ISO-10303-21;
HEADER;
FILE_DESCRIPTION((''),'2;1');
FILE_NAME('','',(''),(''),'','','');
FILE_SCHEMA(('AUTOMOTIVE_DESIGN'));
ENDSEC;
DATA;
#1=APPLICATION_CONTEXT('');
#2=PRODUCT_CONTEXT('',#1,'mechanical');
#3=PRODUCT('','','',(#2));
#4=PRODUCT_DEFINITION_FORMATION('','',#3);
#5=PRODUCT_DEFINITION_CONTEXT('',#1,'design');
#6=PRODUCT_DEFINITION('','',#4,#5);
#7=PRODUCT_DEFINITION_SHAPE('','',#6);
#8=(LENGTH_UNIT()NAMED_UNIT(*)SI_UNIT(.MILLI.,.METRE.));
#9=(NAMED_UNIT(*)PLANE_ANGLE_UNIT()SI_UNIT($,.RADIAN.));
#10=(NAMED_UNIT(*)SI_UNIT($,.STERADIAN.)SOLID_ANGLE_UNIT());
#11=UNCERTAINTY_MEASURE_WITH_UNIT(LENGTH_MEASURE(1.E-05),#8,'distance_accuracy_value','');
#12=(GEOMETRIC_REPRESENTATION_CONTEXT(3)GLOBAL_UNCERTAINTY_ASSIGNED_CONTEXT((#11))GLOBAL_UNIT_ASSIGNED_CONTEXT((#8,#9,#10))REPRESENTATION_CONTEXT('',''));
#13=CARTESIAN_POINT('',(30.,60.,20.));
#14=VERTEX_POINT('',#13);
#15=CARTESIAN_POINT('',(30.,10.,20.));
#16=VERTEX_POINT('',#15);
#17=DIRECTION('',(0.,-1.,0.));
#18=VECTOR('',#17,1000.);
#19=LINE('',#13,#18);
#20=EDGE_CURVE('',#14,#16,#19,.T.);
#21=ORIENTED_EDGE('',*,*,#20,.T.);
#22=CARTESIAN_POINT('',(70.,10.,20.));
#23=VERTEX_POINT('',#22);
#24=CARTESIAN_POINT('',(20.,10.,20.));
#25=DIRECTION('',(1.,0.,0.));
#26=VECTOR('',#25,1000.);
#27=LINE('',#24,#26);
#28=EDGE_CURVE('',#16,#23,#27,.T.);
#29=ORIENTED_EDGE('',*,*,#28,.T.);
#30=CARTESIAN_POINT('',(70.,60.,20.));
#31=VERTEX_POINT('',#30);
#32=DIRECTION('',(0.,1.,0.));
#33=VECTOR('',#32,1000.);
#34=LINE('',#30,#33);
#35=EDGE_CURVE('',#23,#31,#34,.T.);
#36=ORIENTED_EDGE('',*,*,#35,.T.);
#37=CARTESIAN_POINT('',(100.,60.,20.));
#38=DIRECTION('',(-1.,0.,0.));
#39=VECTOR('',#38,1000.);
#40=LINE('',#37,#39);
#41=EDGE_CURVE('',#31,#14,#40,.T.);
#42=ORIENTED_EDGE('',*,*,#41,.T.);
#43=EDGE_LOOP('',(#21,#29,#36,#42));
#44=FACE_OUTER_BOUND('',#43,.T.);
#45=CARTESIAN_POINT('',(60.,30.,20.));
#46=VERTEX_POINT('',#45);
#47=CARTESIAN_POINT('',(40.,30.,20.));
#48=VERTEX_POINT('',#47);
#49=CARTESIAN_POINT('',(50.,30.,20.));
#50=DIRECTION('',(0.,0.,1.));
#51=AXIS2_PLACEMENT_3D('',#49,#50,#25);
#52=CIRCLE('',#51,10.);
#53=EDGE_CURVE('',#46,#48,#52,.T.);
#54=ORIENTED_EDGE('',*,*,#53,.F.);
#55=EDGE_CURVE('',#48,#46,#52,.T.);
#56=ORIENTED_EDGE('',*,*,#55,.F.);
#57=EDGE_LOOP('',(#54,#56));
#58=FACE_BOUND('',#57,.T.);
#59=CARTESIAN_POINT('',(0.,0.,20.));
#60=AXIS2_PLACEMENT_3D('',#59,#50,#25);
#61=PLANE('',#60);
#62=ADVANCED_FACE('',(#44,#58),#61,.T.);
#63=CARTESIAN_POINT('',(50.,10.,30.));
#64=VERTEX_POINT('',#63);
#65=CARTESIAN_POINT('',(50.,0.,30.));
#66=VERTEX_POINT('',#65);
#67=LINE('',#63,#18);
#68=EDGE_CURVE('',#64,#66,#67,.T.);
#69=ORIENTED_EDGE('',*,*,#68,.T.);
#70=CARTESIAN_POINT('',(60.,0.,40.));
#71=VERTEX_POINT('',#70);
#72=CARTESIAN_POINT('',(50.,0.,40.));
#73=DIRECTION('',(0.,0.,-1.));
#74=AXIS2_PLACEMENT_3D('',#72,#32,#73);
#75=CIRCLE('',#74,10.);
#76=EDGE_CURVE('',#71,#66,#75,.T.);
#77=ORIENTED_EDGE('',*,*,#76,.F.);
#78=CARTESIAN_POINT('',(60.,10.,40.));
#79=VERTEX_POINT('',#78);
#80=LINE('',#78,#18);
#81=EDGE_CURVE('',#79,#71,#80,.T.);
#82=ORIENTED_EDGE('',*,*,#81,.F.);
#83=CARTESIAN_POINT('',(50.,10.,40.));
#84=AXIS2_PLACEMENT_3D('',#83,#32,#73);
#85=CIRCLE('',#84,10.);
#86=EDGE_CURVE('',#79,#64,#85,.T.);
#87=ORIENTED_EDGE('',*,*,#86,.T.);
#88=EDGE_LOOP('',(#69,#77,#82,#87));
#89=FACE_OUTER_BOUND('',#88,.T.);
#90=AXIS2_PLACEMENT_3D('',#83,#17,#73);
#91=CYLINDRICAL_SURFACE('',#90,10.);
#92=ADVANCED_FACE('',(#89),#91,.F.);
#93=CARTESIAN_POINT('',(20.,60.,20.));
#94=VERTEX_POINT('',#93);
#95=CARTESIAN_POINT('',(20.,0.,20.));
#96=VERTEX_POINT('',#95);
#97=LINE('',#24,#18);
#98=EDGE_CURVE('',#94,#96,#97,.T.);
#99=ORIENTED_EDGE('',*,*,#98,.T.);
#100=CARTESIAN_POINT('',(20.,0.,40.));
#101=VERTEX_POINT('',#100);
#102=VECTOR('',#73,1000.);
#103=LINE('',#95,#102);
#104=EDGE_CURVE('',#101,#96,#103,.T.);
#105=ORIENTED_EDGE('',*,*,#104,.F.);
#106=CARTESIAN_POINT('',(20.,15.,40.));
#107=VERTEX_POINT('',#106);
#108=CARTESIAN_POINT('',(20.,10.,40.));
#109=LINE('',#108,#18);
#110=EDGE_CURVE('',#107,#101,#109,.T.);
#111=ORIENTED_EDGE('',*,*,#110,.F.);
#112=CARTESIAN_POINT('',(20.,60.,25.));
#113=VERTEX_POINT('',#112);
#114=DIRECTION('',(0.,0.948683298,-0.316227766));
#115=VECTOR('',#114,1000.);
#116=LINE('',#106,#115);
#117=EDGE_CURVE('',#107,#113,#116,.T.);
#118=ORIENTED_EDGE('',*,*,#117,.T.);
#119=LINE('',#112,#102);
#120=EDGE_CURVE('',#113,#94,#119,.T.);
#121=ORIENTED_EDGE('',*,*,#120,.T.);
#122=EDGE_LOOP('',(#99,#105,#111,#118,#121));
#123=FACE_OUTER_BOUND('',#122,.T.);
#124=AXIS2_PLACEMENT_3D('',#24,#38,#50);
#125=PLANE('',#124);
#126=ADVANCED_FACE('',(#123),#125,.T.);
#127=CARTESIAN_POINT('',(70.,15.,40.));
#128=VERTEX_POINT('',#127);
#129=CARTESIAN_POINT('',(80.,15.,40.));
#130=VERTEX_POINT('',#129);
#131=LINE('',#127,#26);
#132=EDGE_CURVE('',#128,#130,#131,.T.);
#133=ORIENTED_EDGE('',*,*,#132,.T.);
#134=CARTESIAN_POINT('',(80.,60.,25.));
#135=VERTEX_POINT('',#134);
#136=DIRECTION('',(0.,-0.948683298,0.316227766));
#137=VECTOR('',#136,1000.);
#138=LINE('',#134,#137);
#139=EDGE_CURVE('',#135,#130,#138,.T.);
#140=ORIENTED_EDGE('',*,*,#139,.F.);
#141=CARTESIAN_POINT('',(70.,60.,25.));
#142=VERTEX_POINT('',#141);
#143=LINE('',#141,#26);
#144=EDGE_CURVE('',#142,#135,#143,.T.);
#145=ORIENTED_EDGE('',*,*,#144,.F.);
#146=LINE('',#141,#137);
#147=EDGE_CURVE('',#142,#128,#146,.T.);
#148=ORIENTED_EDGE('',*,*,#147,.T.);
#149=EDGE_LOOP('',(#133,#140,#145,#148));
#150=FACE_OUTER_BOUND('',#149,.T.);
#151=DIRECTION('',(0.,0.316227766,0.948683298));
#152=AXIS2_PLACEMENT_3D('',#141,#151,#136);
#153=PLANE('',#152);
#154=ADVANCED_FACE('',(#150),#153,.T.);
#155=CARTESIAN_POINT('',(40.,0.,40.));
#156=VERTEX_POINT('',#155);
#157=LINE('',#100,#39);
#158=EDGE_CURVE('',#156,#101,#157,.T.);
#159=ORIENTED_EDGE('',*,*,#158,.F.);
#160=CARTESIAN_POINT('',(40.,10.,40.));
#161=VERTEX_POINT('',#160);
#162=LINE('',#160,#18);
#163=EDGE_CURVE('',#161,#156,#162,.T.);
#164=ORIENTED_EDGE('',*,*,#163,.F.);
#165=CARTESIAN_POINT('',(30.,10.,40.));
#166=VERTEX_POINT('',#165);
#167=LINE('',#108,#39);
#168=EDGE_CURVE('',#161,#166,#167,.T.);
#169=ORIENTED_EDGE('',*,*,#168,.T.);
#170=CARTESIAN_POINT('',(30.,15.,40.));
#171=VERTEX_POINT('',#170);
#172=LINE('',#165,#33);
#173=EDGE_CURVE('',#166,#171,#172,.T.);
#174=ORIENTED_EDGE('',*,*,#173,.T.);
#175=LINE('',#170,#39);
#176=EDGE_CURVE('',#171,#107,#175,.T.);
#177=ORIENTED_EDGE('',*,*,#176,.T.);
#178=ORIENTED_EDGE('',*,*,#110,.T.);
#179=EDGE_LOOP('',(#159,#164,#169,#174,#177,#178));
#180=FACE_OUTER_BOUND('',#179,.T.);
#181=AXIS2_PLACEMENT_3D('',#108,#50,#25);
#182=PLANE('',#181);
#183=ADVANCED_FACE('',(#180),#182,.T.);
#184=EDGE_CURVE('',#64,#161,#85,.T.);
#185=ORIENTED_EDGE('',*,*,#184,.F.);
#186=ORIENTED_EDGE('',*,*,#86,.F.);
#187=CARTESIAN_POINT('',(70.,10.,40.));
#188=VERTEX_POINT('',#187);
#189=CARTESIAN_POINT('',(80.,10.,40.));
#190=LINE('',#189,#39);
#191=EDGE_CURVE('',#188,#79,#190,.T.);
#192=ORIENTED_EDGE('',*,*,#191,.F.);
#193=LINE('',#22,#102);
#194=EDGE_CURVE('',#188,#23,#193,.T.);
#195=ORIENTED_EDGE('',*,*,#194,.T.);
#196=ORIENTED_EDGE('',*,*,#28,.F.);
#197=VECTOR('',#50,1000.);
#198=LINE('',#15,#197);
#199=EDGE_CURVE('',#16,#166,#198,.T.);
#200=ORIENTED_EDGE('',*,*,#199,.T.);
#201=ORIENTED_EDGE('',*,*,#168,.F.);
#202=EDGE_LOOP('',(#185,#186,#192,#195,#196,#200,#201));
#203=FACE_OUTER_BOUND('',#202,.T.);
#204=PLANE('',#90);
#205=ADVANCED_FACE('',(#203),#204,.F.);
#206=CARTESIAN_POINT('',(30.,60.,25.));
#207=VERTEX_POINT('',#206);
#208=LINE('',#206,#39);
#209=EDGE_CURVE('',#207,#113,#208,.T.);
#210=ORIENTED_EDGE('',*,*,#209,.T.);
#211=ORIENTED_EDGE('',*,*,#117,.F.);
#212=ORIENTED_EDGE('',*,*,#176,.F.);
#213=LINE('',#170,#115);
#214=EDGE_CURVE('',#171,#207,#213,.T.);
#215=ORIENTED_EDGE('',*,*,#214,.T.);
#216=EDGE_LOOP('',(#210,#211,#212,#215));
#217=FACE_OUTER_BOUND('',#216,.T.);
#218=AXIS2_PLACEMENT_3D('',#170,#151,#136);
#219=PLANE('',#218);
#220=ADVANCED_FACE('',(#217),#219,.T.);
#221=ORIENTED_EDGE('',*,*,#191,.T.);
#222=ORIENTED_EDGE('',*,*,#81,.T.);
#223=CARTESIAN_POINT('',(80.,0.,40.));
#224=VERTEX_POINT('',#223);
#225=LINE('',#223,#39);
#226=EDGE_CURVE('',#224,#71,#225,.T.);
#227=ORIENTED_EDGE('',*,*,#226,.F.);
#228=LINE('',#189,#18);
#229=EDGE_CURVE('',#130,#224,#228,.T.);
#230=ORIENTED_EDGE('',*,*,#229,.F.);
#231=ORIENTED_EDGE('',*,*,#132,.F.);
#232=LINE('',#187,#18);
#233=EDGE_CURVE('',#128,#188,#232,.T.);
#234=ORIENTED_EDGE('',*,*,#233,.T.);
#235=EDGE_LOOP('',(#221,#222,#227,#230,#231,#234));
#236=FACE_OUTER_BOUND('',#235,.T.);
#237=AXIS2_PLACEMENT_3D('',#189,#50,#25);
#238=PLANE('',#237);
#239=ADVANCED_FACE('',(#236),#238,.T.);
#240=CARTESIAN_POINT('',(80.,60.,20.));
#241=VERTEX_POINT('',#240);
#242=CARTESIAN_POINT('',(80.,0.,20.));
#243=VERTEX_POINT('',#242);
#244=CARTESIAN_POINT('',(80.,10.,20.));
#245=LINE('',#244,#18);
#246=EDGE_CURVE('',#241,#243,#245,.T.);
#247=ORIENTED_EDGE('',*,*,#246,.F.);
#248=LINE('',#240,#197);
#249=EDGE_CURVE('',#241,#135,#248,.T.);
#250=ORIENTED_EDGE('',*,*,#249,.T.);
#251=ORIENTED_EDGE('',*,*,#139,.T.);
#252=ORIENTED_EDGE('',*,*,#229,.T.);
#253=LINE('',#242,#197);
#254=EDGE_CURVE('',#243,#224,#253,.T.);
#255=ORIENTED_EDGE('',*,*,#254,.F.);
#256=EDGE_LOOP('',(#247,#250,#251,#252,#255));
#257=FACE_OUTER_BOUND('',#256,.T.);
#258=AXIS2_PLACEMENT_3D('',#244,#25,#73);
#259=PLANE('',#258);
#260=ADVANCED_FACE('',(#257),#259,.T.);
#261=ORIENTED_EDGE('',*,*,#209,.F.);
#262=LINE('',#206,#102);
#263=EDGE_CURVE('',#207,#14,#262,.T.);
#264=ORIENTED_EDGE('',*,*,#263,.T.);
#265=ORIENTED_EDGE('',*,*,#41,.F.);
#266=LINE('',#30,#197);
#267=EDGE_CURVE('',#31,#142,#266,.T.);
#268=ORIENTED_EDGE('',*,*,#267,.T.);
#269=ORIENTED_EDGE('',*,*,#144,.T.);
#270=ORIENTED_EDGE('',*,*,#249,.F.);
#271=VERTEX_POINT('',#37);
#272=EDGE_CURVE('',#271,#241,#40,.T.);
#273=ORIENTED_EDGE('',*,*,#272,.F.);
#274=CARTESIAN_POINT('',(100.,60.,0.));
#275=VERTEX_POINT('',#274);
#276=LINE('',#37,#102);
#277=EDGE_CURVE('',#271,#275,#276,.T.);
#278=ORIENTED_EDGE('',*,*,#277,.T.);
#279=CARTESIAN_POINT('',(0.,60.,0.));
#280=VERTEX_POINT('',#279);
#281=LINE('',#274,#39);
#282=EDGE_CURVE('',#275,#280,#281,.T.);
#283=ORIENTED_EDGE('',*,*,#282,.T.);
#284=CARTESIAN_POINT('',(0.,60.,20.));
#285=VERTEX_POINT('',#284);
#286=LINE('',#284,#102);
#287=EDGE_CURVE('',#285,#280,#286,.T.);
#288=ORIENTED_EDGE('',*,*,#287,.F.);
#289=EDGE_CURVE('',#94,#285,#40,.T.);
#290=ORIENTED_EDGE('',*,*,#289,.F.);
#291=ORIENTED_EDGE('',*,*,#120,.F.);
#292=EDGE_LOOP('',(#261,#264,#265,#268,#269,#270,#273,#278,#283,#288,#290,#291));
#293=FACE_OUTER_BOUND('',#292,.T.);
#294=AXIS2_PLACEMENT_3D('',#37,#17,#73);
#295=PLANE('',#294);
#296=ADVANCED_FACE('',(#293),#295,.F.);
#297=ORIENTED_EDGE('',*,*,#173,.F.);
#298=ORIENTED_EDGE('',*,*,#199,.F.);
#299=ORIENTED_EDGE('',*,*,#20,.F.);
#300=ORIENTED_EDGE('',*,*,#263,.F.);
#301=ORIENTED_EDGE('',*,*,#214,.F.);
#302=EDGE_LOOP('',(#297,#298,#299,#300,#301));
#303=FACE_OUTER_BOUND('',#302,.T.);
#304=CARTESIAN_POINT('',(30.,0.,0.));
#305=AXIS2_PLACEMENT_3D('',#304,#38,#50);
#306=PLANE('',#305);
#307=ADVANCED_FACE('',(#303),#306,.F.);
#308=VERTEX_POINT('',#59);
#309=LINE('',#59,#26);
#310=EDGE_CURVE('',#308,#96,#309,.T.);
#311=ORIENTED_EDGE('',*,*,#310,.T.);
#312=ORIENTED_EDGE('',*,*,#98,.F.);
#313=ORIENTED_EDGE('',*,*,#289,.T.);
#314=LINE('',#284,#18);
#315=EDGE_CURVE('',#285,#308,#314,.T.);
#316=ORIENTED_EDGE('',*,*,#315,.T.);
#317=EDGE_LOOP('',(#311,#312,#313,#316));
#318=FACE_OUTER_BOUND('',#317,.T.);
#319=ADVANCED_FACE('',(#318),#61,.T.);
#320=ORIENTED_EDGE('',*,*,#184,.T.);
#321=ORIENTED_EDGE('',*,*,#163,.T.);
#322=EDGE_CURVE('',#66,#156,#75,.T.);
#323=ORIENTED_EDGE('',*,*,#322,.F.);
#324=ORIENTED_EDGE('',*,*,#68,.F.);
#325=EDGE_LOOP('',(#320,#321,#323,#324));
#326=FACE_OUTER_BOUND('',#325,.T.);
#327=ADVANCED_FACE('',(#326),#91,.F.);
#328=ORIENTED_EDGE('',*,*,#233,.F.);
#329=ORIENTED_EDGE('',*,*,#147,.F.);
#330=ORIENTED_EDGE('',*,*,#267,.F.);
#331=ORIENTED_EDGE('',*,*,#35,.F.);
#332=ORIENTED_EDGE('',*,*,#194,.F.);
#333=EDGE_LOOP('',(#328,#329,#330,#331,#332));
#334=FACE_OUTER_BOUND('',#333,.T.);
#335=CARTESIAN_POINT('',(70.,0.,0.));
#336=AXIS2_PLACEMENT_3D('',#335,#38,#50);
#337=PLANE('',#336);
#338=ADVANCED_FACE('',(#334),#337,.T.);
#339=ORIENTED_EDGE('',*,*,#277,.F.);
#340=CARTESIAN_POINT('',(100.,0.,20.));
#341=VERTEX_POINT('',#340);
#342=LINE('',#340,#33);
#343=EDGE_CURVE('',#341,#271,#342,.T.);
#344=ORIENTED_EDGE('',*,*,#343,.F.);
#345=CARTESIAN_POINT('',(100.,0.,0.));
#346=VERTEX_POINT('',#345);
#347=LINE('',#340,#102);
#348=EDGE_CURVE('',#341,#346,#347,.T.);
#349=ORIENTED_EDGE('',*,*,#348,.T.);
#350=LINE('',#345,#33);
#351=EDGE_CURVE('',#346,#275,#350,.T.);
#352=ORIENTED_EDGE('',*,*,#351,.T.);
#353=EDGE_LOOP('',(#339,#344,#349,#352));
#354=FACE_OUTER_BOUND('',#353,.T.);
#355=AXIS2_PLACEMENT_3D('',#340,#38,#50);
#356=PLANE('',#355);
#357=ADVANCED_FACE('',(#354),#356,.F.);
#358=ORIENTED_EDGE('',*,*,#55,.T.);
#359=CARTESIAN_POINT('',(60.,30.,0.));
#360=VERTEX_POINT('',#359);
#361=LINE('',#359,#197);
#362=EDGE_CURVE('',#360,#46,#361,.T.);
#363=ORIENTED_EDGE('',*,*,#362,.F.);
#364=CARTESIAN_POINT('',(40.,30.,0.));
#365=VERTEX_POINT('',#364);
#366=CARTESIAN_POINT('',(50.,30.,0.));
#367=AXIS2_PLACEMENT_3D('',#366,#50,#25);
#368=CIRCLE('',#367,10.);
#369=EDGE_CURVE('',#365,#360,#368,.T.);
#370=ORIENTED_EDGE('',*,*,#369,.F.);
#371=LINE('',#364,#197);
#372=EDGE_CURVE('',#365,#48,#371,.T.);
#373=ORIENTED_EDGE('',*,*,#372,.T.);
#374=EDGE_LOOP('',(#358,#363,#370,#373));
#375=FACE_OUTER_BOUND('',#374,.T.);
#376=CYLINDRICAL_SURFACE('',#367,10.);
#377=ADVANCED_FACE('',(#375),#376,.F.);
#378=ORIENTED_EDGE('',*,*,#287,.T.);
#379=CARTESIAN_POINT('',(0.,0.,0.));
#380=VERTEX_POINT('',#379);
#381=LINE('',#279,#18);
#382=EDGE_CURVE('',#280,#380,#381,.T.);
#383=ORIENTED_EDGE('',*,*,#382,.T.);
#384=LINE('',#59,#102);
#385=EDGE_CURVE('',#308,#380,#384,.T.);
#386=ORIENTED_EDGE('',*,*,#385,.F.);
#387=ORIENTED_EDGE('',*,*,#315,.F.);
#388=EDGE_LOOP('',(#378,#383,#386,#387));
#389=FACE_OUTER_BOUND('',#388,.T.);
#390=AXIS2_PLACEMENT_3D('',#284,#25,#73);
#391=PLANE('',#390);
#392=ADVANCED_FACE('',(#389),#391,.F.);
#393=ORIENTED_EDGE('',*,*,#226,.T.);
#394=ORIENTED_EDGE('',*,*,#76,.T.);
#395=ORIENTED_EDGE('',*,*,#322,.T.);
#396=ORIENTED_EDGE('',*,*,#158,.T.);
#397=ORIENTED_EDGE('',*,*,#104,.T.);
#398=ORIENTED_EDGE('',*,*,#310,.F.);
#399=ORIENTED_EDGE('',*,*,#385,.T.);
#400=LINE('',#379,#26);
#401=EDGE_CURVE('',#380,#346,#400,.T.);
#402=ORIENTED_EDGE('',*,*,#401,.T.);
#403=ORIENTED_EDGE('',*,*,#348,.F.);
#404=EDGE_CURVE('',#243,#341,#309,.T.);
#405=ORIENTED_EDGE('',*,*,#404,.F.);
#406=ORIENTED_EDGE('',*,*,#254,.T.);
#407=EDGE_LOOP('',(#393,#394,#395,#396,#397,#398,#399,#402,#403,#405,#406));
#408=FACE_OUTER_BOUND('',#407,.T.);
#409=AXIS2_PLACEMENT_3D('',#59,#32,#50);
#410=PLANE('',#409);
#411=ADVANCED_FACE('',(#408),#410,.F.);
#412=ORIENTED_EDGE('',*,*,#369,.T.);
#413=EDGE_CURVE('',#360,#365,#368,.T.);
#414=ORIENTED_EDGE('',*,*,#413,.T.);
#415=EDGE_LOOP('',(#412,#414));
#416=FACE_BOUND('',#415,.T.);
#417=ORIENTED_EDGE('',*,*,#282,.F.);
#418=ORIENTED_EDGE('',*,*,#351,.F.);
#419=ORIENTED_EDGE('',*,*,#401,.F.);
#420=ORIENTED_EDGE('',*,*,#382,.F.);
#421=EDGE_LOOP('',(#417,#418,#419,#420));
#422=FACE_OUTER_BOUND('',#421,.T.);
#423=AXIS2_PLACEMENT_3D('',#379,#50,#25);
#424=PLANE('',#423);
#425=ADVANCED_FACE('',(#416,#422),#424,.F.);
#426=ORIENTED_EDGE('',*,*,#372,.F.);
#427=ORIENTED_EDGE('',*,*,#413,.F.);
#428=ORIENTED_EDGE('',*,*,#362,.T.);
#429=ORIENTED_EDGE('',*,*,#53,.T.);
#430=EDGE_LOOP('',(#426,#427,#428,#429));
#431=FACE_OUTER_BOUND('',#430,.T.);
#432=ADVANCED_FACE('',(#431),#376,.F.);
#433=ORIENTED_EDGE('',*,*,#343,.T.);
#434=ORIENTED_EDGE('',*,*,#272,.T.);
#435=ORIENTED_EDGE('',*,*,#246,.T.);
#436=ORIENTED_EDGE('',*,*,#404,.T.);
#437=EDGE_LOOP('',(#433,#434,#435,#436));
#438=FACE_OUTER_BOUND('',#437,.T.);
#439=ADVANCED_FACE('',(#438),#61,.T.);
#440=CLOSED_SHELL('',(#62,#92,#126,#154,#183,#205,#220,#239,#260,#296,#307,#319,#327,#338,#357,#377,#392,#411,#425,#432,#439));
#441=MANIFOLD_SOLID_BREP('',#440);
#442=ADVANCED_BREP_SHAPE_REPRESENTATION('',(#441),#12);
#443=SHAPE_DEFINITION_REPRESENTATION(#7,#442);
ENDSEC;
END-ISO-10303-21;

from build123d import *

# Parameters (mm, degrees)
BACK_PLATE_SKETCH_W       = 100
BACK_PLATE_SKETCH_H       = 60
BACK_PLATE_DEPTH          = 20
BORE_20_SKETCH_R          = 10
BORE_20_DEPTH             = 20
NOTCHED_BASE_FLANGE_DEPTH = 10
LEFT_GUSSET_DEPTH         = 10
RIGHT_GUSSET_DEPTH        = 10


with BuildPart() as part:
    # Back Plate Sketch → Back Plate (new body)
    with BuildSketch(Plane.XY):
        with Locations((50, 30)):
            Rectangle(BACK_PLATE_SKETCH_W, BACK_PLATE_SKETCH_H)
    extrude(amount=BACK_PLATE_DEPTH)

    # Bore Ø20 Sketch → Bore Ø20 (cut)
    with BuildSketch(Plane.XY.offset(20)):
        with Locations((50, 30)):
            Circle(BORE_20_SKETCH_R)
    extrude(amount=-BORE_20_DEPTH, mode=Mode.SUBTRACT)

    # Base Flange Sketch → Notched Base Flange (add)
    with BuildSketch(Plane.XZ):
        with BuildLine():
            Line((20, 20), (20, 40))
            Line((20, 40), (40, 40))
            ThreePointArc((40, 40), (50, 30), (60, 40))
            Line((60, 40), (80, 40))
            Line((80, 40), (80, 20))
            Line((80, 20), (20, 20))
        make_face()
    extrude(amount=-NOTCHED_BASE_FLANGE_DEPTH)

    # Left Gusset Sketch → Left Gusset (add)
    with BuildSketch(Plane(origin=(80, 0, 0), x_dir=(0, 0, -1), z_dir=(1, 0, 0))):
        Polygon((-40, 10), (-40, 15), (-25, 60), (-20, 60), (-20, 10), align=None)
    extrude(amount=-LEFT_GUSSET_DEPTH)

    # Right Gusset Sketch → Right Gusset (add)
    with BuildSketch(Plane.ZY.offset(-20)):
        Polygon((40, 10), (40, 15), (25, 60), (20, 60), (20, 10), align=None)
    extrude(amount=-RIGHT_GUSSET_DEPTH)


solid = part.part
